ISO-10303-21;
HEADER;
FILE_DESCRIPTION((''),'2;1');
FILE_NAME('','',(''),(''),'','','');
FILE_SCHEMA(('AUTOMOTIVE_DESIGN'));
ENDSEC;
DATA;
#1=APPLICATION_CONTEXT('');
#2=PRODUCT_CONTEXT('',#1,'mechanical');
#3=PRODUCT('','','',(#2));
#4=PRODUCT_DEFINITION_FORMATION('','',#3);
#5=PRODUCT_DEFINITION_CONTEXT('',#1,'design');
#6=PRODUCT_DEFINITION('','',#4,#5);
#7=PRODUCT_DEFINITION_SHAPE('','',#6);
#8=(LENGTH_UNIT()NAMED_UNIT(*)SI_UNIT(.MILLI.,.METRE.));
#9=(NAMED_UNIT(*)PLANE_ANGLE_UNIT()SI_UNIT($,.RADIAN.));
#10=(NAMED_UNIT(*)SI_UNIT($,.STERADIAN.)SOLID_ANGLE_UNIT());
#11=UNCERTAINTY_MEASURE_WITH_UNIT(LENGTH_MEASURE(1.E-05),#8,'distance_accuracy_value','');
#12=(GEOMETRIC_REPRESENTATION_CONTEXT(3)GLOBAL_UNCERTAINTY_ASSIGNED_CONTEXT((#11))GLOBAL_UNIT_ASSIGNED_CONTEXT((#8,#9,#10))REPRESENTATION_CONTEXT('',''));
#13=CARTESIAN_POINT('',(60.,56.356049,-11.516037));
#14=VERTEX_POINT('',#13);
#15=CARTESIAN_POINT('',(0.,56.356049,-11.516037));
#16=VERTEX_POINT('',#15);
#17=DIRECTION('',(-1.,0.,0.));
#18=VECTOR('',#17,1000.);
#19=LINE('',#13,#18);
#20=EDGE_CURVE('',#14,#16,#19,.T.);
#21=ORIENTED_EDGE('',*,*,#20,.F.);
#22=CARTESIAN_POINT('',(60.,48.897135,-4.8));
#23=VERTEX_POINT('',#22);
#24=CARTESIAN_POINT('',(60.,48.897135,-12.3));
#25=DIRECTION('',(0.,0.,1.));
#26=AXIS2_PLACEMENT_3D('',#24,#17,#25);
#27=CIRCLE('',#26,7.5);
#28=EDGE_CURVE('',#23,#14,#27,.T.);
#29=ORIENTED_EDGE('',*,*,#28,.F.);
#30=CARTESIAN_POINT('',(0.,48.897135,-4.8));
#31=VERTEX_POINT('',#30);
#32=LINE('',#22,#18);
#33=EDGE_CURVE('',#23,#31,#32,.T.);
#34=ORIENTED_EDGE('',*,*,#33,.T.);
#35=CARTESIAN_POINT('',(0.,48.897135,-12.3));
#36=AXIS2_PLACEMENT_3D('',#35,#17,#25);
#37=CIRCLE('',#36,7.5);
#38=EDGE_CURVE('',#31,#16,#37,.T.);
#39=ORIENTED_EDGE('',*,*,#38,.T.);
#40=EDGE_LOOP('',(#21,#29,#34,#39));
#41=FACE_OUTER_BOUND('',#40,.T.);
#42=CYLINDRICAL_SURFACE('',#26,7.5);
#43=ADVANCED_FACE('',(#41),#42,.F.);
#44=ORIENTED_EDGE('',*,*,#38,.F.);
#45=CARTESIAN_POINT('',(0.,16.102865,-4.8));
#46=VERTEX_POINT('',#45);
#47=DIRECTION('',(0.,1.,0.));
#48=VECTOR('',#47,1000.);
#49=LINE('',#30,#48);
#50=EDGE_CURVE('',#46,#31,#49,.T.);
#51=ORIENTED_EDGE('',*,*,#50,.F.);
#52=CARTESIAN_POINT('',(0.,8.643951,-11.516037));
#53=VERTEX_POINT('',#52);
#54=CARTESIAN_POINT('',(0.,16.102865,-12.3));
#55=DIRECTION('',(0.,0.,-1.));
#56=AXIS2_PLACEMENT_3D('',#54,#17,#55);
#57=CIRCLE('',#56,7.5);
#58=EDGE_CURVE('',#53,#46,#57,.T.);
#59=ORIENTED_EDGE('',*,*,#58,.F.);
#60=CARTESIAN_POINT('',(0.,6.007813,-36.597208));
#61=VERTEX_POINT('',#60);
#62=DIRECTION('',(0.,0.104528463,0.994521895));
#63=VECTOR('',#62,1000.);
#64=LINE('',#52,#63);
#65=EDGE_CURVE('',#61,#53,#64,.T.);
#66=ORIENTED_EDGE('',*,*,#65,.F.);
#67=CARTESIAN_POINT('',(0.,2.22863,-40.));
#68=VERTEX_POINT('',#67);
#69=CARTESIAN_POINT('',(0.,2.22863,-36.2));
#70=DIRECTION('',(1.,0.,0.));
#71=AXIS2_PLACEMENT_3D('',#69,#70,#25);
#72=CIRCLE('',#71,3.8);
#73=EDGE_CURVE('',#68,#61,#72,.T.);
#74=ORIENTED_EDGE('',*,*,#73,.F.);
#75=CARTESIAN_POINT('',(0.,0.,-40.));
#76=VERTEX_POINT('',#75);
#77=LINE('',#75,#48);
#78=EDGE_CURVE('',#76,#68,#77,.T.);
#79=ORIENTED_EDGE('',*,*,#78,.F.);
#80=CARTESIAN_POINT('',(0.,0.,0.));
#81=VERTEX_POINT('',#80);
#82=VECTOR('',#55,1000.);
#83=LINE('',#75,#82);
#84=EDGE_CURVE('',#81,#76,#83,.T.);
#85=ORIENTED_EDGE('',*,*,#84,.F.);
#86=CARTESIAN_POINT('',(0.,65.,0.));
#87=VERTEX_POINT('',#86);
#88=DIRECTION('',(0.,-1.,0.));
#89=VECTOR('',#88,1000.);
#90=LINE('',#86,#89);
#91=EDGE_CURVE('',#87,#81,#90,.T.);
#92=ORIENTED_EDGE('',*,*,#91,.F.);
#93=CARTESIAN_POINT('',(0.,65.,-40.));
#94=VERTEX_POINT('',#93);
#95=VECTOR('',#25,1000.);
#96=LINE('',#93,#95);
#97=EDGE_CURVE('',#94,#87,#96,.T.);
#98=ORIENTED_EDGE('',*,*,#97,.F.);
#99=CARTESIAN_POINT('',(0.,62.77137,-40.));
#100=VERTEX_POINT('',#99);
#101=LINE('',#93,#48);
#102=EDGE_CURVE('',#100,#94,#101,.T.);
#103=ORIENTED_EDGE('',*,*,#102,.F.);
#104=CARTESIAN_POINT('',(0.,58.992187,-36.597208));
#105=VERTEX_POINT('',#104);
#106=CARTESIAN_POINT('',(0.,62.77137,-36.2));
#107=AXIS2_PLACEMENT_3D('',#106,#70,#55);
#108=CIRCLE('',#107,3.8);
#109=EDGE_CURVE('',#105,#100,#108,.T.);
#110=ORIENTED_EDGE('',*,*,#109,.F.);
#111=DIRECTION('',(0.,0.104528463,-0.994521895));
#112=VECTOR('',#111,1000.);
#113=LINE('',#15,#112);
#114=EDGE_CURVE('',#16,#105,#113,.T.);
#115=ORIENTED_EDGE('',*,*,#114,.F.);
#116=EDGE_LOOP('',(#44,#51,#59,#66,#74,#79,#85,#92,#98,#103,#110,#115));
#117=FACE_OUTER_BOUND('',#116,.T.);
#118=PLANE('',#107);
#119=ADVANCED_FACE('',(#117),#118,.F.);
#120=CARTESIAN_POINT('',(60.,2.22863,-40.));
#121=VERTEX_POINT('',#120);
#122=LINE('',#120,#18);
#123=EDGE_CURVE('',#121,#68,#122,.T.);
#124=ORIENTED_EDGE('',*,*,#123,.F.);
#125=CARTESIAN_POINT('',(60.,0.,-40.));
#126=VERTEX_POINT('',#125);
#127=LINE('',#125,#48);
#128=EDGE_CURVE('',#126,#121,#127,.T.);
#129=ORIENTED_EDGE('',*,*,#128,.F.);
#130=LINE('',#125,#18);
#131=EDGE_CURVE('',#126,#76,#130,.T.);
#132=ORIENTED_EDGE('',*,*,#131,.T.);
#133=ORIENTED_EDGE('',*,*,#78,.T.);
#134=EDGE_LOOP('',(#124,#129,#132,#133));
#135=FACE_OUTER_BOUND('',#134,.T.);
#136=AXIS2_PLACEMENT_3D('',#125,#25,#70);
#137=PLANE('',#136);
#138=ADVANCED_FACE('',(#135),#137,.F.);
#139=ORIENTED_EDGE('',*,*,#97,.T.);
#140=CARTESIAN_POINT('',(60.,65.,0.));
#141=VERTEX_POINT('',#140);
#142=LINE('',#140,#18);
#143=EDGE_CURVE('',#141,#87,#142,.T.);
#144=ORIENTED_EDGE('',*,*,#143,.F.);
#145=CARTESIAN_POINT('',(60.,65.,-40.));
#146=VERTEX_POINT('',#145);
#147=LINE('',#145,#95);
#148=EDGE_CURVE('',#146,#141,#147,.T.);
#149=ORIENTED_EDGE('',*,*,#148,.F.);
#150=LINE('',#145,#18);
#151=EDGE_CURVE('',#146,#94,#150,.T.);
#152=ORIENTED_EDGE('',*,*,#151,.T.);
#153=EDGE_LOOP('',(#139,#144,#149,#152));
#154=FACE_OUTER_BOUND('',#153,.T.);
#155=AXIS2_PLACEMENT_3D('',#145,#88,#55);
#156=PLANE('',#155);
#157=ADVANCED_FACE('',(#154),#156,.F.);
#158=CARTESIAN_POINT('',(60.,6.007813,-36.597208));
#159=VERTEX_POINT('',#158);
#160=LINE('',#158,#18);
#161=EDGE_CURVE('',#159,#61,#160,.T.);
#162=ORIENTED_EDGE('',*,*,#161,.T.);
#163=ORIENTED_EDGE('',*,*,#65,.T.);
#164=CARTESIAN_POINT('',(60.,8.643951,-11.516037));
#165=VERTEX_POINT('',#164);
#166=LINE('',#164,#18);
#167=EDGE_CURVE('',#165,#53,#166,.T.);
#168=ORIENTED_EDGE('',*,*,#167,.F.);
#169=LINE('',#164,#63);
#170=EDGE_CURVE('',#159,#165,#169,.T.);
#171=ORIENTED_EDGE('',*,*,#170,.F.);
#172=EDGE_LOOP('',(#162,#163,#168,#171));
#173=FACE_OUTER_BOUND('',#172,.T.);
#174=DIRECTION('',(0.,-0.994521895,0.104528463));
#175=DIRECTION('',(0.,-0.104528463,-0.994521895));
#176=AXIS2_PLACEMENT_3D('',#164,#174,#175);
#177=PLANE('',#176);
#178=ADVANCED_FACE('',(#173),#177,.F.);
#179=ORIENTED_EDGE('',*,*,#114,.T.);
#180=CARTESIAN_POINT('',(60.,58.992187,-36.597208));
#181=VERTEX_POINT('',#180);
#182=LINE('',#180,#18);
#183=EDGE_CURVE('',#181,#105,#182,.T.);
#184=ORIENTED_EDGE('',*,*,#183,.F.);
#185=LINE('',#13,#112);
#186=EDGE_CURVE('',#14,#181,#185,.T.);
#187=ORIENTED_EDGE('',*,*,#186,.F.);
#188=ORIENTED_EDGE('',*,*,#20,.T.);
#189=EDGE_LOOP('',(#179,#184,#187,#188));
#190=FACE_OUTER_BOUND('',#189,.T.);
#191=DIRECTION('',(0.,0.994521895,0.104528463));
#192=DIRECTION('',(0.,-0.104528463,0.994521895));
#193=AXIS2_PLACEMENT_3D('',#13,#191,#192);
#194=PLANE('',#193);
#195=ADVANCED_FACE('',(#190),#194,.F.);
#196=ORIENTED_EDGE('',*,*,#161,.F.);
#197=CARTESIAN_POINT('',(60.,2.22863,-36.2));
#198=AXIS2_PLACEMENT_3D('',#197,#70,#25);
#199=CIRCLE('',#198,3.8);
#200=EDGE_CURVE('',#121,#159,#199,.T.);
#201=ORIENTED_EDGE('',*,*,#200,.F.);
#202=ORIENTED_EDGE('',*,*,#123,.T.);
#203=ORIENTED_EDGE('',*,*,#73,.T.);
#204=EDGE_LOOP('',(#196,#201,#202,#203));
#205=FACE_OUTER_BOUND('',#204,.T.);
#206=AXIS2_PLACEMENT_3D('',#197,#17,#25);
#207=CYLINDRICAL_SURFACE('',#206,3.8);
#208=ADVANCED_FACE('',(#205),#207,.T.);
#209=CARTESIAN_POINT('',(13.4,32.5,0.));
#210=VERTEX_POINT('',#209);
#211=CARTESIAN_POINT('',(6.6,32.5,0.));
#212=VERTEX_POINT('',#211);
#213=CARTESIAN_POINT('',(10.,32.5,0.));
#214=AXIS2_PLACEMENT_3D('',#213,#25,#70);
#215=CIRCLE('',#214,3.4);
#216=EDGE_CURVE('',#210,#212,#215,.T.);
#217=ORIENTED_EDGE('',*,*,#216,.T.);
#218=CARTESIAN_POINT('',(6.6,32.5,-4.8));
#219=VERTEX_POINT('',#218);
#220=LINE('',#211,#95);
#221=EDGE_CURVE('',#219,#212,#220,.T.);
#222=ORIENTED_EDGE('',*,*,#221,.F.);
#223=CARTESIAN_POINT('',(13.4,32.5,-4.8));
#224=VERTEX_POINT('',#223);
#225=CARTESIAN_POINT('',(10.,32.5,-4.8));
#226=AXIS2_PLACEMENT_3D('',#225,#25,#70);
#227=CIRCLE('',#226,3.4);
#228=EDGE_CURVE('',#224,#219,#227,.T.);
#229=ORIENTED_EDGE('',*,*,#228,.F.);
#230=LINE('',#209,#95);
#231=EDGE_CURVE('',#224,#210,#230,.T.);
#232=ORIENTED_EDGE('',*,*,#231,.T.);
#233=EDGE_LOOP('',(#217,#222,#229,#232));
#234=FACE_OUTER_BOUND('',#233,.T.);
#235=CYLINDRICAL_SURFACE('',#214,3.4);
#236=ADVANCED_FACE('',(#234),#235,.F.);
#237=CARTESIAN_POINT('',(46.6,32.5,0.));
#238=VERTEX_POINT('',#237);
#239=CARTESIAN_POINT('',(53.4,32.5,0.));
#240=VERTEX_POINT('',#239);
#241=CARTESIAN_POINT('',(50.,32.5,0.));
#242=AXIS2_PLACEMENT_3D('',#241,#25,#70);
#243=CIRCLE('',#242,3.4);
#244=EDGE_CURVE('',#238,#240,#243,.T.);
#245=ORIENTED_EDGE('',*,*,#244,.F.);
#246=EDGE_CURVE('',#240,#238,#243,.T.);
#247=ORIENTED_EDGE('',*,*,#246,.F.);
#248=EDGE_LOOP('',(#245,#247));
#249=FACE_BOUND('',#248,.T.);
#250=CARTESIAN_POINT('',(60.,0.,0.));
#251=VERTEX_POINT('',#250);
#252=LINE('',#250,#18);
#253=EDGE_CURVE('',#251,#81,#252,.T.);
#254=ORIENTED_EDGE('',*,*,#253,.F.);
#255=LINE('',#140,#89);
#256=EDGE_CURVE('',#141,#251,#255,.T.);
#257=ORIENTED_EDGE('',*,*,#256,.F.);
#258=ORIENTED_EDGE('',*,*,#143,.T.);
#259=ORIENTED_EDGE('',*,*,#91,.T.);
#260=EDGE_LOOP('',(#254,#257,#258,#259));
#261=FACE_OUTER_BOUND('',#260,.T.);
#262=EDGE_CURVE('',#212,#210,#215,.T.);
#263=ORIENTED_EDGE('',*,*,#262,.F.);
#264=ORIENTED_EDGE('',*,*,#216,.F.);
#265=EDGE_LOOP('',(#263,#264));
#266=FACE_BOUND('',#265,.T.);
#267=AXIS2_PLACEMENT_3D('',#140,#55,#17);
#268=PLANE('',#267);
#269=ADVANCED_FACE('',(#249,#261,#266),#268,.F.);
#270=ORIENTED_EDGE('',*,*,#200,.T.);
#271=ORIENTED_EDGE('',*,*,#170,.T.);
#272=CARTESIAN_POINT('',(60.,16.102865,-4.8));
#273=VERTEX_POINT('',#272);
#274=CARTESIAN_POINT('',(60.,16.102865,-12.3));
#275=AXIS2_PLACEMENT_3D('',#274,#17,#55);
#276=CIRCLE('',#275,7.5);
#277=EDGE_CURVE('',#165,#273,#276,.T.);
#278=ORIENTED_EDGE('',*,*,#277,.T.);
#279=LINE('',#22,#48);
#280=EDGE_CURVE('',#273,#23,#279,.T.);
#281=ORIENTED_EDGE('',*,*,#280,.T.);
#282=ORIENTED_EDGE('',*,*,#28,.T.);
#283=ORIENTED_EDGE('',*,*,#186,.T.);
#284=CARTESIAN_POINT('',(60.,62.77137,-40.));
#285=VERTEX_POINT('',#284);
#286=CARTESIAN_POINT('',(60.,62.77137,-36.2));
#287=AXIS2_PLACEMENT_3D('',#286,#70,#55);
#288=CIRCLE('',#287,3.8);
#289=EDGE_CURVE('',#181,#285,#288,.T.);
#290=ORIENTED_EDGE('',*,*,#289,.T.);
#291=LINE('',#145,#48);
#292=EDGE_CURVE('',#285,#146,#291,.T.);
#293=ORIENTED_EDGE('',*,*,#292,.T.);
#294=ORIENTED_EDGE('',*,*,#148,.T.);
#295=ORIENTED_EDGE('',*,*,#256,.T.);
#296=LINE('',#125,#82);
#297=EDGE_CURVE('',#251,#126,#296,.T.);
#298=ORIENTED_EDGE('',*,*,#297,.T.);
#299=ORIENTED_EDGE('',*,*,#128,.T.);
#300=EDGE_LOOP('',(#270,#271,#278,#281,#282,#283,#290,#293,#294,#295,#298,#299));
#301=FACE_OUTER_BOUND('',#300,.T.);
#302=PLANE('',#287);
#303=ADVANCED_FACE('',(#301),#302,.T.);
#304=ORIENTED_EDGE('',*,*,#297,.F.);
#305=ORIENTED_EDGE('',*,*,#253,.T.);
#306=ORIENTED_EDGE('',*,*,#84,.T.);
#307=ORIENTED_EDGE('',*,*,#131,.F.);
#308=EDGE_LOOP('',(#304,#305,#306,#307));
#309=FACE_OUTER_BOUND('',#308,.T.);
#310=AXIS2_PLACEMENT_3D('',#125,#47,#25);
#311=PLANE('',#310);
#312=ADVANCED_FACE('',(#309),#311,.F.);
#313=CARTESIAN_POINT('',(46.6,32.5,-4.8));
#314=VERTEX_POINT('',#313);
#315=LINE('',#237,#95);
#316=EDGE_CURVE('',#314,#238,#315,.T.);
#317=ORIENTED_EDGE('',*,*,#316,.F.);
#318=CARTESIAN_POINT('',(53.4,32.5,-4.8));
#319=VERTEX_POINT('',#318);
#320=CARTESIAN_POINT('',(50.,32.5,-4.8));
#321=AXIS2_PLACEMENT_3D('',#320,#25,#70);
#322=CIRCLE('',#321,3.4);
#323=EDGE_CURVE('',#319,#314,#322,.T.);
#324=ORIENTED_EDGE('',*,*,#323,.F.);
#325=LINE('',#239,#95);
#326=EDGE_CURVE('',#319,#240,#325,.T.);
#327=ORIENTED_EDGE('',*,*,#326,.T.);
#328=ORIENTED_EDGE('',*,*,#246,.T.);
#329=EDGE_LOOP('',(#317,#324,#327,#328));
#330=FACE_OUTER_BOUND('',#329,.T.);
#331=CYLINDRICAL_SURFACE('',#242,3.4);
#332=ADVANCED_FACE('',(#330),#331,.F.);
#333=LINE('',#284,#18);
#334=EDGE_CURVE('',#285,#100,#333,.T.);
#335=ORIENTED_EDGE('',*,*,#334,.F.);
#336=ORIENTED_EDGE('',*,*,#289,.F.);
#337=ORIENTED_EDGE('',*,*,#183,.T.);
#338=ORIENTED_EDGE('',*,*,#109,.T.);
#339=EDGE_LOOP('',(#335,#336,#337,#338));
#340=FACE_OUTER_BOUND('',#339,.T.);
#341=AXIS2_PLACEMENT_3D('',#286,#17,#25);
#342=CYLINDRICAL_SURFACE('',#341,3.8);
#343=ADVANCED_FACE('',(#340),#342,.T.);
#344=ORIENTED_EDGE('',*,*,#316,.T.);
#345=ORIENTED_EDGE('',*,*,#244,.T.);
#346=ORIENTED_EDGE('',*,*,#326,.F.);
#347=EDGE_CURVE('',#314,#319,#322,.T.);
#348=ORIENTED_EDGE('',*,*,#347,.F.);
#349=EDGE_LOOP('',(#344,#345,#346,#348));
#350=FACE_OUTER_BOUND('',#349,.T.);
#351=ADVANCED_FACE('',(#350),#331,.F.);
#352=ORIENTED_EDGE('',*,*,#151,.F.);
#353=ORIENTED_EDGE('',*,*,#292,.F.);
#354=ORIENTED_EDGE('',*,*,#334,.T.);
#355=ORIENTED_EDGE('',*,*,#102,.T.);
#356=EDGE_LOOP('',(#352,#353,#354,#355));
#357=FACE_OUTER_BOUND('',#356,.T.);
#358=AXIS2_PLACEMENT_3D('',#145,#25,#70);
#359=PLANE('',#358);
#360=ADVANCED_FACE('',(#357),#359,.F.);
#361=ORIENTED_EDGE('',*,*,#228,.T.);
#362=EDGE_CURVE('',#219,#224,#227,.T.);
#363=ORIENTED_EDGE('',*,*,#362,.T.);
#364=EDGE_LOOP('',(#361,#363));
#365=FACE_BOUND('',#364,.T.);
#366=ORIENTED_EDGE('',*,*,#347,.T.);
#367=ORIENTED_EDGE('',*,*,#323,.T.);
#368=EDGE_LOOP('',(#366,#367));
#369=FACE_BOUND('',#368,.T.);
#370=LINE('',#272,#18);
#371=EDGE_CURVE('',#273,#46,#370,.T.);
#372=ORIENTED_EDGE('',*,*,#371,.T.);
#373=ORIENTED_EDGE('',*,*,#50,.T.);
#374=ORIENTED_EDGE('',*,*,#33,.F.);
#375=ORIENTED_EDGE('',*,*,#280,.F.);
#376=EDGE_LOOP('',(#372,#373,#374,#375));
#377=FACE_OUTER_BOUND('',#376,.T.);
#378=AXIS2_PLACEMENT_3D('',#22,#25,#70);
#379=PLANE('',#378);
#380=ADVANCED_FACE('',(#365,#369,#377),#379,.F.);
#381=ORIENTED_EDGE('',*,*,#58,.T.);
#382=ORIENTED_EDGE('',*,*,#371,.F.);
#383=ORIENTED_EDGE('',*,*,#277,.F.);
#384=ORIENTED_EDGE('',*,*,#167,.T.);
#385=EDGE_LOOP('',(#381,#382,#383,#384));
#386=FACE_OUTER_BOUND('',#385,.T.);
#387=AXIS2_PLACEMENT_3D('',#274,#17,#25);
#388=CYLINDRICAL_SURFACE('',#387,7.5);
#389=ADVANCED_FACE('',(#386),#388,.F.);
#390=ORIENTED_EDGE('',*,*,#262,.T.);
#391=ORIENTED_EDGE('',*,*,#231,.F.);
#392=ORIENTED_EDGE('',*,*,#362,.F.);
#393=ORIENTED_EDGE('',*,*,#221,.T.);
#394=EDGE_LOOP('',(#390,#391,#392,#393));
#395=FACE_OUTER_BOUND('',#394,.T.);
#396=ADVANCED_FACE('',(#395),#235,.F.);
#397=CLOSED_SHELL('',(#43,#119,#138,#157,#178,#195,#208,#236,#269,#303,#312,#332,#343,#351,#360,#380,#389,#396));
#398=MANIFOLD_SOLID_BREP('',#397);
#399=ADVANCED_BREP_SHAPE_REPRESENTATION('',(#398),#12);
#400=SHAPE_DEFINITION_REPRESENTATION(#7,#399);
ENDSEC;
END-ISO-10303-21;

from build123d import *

# Parameters (mm, degrees)
MEMBER_C_6_5_1_DEPTH = 60
HOLE_WIZARD_M8_1_D   = 6.8


with BuildPart() as part:
    # Sketch11 → Member C _ 6.5_1 (new body)
    with BuildSketch(Plane(origin=(0, 0, 0), x_dir=(0, 0, -1), z_dir=(1, 0, 0))):
        with BuildLine():
            Line((40, 65), (0, 65))
            Line((0, 65), (0, 0))
            Line((0, 0), (40, 0))
            Line((40, 0), (40, 2.228630091))
            ThreePointArc((40, 2.228630091), (39.023950337, 4.771326395), (36.59720816, 6.007813293))
            Line((36.59720816, 6.007813293), (11.516036525, 8.643950658))
            ThreePointArc((11.516036525, 8.643950658), (6.726413809, 11.084385325), (4.8, 16.102864873))
            Line((4.8, 16.102864873), (4.8, 48.897135127))
            ThreePointArc((4.8, 48.897135127), (6.726413809, 53.915614675), (11.516036525, 56.356049342))
            Line((11.516036525, 56.356049342), (36.59720816, 58.992186707))
            ThreePointArc((36.59720816, 58.992186707), (39.023950337, 60.228673605), (40, 62.771369909))
            Line((40, 62.771369909), (40, 65))
        make_face()
    extrude(amount=MEMBER_C_6_5_1_DEPTH)

    # M8 螺纹孔1 (through all)
    with Locations(Plane(origin=(10, 32.5, 0), x_dir=(1, 0, 0), z_dir=(0, 0, 1))):
        with Locations((0, 0), (40, 0)):
            Hole(HOLE_WIZARD_M8_1_D / 2)


solid = part.part
